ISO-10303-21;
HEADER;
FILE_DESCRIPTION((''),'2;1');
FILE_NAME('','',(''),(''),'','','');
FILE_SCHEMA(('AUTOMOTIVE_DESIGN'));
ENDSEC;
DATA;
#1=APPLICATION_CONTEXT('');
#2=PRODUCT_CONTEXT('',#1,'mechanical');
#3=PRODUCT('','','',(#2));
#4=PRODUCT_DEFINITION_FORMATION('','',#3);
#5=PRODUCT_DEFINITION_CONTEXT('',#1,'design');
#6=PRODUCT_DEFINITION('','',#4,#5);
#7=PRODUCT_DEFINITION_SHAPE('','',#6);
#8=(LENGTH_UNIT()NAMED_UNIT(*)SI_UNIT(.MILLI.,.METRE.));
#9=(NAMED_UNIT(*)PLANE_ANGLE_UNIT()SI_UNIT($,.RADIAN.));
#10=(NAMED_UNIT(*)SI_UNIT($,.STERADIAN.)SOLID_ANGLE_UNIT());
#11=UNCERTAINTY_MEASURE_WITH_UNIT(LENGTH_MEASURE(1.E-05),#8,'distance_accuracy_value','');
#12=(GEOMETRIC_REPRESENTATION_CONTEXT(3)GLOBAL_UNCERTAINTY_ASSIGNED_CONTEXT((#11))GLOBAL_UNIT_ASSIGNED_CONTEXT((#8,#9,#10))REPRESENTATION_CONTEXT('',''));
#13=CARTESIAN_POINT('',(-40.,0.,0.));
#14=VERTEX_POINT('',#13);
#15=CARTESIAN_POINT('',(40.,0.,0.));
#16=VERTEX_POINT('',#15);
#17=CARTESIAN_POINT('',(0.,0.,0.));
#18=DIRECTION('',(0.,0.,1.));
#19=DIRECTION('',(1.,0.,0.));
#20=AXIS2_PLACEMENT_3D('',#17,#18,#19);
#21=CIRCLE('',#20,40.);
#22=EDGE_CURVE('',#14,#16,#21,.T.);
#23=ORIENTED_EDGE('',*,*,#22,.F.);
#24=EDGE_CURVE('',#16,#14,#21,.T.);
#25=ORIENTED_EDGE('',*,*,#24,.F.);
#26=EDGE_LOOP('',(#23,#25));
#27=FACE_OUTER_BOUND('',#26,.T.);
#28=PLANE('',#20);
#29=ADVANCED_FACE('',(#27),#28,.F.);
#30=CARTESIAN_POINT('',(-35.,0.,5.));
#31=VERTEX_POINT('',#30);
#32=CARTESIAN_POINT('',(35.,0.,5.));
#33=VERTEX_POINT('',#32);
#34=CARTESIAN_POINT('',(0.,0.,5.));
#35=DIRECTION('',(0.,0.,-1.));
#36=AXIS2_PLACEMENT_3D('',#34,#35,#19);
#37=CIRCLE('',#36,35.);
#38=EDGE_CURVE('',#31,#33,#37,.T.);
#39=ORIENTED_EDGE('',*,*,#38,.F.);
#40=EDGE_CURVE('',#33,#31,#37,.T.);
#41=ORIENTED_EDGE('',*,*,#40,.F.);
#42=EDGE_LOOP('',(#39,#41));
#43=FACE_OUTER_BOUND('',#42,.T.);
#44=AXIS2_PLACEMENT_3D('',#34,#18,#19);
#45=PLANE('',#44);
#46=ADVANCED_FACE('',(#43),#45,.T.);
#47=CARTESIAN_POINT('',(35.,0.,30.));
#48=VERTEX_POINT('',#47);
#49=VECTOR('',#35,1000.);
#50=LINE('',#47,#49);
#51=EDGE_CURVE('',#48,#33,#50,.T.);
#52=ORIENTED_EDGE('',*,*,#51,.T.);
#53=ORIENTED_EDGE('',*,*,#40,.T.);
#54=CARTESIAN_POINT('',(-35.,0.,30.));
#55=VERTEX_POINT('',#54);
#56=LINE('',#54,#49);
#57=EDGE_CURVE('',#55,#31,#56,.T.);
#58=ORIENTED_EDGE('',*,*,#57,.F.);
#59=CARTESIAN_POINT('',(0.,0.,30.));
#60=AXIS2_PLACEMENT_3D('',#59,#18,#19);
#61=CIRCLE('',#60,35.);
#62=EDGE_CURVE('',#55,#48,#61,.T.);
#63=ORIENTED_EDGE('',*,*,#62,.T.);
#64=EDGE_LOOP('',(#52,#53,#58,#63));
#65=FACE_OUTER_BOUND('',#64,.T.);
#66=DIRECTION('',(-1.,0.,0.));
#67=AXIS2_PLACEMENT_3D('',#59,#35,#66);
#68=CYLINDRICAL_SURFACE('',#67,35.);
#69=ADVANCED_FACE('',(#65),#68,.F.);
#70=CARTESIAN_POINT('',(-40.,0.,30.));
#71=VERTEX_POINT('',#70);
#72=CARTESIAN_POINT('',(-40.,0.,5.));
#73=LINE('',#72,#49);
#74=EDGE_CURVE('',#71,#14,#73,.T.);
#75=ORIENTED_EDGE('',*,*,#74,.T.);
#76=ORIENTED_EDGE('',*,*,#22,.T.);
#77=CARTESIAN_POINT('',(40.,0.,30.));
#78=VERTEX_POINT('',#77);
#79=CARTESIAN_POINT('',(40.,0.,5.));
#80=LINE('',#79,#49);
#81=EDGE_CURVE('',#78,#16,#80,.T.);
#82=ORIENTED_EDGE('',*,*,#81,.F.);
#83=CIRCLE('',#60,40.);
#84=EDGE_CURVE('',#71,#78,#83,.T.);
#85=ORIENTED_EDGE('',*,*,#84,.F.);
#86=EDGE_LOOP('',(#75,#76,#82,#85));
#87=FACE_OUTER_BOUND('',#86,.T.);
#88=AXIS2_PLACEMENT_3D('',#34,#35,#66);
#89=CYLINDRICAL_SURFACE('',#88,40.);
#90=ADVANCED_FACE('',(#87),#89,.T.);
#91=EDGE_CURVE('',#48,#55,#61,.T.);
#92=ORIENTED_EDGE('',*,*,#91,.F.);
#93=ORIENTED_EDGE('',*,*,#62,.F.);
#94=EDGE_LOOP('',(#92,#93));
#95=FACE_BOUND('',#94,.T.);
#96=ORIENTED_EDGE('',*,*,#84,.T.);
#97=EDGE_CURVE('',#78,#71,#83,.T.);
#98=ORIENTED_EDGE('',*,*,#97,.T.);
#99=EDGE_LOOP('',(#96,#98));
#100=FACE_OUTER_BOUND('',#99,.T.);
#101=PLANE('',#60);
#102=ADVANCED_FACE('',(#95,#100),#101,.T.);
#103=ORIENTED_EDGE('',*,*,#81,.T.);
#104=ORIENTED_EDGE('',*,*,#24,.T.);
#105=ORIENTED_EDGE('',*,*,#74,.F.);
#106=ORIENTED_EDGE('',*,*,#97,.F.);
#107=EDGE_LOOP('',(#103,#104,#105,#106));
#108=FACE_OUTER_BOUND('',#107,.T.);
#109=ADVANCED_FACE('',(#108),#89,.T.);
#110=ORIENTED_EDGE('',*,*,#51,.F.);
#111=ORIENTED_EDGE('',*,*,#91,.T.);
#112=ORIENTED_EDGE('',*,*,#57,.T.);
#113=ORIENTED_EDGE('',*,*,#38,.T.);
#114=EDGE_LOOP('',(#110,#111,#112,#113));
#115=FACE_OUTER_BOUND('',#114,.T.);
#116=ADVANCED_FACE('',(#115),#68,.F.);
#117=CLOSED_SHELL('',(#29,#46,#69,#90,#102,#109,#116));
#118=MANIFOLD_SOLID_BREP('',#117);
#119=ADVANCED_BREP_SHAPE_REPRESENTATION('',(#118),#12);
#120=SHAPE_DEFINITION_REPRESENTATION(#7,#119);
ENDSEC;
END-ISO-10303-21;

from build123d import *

# Parameters (mm, degrees)
SKETCH1_R           = 40
BOSS_EXTRUDE1_DEPTH = 5
SKETCH2_R           = 40
SKETCH2_R_2         = 35
BOSS_EXTRUDE2_DEPTH = 25


with BuildPart() as part:
    # Sketch1 → Boss-Extrude1 (new body)
    with BuildSketch(Plane.XY):
        Circle(SKETCH1_R)
    extrude(amount=BOSS_EXTRUDE1_DEPTH)

    # Sketch2 → Boss-Extrude2 (add)
    with BuildSketch(Plane.XY.offset(5)):
        Circle(SKETCH2_R)
        Circle(SKETCH2_R_2, mode=Mode.SUBTRACT)
    extrude(amount=BOSS_EXTRUDE2_DEPTH)


solid = part.part
